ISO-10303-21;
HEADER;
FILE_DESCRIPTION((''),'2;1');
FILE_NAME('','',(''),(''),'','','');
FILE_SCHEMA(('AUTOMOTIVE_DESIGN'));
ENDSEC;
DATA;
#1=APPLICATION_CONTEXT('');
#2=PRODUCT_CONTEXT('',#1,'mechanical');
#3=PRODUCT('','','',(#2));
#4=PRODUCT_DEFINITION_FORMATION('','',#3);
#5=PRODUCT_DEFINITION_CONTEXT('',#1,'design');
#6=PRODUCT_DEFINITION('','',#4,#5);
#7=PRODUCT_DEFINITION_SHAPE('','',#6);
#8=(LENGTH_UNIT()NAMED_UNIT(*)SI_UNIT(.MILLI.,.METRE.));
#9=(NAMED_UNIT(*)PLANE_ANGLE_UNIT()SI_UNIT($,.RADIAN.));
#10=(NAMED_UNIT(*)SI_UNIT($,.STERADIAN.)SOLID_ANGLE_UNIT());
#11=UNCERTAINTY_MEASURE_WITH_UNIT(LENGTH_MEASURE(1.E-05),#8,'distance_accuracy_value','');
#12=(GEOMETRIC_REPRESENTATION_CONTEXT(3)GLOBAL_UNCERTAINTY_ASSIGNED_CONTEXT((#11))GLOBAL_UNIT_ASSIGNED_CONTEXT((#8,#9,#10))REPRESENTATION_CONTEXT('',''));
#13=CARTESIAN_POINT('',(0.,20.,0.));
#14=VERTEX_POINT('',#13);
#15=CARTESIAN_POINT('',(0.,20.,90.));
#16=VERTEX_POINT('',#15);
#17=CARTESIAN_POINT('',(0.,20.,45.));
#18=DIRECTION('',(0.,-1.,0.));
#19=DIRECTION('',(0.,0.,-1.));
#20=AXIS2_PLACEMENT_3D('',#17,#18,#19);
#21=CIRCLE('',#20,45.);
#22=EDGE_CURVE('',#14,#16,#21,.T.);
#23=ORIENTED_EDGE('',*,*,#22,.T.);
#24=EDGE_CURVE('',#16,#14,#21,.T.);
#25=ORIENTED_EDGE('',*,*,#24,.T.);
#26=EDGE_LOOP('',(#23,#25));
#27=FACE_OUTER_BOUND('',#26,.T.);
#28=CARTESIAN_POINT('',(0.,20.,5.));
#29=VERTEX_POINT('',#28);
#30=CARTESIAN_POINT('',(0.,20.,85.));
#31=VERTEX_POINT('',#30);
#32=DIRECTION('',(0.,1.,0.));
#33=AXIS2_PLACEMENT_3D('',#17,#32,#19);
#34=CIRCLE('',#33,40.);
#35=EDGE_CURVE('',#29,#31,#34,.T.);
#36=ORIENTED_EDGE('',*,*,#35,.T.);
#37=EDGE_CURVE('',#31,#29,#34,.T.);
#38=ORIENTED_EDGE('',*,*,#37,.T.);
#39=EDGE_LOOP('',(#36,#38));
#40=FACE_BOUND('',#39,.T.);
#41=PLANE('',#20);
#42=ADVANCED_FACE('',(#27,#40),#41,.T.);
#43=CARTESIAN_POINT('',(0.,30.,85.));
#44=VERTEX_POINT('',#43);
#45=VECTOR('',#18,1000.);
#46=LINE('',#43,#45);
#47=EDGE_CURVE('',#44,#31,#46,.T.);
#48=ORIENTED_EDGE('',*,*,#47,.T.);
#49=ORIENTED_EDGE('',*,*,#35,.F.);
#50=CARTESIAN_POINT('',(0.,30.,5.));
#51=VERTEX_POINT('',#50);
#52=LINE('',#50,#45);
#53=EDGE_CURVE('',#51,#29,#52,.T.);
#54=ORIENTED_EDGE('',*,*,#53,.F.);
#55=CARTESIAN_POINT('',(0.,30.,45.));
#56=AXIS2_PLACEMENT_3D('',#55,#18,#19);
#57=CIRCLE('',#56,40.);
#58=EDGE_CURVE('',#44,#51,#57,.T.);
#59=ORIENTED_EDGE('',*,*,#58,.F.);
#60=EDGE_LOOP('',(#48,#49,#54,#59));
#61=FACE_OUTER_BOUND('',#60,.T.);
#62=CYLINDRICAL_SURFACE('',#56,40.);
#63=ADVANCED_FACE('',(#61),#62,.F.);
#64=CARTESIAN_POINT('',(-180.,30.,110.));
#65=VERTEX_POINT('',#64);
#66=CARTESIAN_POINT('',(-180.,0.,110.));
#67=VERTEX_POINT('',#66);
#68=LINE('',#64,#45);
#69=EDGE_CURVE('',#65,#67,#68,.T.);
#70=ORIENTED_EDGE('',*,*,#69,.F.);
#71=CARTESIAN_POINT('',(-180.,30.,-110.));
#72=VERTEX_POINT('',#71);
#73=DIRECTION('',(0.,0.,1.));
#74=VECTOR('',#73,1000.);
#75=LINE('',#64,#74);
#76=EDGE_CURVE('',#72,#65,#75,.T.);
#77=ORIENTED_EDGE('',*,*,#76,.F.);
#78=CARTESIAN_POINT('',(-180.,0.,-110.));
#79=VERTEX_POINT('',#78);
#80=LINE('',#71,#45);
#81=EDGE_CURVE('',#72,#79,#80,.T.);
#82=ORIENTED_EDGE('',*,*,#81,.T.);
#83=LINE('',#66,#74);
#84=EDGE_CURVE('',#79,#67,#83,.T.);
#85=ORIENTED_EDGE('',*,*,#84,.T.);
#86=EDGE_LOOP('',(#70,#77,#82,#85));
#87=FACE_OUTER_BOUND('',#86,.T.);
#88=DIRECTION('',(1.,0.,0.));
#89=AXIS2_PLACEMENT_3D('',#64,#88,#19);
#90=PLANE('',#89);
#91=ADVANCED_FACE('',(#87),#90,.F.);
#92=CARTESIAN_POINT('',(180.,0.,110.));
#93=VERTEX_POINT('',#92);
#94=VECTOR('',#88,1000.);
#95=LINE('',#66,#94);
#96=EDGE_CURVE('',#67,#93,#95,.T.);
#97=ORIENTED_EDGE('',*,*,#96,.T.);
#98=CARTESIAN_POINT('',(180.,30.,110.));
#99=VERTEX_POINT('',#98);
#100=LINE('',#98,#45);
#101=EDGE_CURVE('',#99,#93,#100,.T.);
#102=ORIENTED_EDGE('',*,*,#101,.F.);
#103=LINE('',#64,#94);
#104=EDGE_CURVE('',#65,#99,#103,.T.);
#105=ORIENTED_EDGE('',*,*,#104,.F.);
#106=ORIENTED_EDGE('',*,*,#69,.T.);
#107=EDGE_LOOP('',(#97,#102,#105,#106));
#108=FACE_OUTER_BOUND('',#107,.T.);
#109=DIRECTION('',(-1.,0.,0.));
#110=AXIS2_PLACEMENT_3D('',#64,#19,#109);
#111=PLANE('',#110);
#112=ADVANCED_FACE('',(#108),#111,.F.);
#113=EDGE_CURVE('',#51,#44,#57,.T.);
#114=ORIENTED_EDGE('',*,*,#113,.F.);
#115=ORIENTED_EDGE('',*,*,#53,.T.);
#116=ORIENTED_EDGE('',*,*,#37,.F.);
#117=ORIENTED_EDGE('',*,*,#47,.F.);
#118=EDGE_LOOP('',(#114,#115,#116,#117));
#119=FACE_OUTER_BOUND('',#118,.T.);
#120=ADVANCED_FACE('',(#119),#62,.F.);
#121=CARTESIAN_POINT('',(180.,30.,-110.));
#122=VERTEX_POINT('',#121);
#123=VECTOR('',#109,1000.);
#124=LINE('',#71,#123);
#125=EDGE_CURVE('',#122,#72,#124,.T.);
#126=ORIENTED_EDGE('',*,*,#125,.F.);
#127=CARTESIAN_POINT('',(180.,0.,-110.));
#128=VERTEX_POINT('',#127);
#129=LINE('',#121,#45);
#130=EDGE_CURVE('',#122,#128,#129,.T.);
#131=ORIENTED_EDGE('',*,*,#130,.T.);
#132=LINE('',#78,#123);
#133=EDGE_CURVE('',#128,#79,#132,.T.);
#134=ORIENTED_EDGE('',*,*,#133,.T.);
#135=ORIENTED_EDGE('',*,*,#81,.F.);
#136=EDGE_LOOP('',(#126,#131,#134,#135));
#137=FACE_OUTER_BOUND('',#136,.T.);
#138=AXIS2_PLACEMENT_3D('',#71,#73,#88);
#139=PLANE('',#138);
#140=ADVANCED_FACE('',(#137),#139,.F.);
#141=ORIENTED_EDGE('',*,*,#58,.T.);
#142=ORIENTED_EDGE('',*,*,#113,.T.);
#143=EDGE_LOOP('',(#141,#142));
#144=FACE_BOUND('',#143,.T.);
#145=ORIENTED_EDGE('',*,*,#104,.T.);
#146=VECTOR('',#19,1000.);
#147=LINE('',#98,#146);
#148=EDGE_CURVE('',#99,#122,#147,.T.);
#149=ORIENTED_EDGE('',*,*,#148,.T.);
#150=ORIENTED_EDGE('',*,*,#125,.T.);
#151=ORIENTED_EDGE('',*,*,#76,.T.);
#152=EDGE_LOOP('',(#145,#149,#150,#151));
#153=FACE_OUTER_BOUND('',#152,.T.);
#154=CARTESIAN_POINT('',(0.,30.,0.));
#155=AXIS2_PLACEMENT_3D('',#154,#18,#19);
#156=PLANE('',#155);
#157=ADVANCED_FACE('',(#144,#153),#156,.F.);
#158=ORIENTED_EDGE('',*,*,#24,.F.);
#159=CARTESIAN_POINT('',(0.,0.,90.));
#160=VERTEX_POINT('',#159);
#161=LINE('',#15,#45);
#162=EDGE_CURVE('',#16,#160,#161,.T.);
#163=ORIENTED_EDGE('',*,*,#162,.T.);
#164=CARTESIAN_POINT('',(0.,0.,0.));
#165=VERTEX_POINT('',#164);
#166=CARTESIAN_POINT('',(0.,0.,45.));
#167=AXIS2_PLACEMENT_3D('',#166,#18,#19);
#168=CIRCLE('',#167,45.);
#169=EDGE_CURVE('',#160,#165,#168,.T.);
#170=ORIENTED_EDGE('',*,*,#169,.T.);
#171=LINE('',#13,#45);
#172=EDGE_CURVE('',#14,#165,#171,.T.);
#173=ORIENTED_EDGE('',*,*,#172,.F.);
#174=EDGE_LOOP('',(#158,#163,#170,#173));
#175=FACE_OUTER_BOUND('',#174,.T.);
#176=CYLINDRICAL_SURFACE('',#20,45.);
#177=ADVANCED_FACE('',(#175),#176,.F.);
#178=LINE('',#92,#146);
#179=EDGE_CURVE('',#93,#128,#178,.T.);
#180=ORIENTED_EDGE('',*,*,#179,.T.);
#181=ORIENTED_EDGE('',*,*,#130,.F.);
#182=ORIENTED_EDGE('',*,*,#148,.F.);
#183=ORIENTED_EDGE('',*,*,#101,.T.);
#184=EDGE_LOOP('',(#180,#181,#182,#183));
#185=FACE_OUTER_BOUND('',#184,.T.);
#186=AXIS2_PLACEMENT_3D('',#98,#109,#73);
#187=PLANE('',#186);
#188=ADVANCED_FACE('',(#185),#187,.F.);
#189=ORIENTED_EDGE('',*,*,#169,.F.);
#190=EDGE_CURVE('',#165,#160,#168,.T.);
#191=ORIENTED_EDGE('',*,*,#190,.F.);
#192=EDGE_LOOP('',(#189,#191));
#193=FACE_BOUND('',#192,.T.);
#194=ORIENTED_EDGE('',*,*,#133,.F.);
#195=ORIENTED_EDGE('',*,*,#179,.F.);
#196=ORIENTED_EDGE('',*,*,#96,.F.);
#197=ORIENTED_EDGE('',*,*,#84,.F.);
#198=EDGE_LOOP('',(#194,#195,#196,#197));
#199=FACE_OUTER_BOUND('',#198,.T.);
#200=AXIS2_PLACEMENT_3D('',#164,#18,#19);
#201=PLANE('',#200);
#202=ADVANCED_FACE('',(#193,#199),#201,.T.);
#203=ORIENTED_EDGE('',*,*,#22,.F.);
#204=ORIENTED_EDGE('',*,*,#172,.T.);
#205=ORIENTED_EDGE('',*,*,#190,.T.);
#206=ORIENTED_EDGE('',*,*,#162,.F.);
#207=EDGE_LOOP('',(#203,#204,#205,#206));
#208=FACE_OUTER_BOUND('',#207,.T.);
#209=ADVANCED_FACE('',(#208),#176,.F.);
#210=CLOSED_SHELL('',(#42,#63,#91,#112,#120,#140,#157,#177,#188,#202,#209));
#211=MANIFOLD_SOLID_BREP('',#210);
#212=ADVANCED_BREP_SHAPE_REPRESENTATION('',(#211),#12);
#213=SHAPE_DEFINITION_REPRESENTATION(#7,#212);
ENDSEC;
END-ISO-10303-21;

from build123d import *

# Parameters (mm, degrees)
SKETCH_1_W          = 360
SKETCH_1_H          = 220
EXTRUDE_1_DEPTH     = 30
SKETCH_2_R          = 40
CUT_EXTRUDE_1_DEPTH = 214.072757527
SKETCH_4_R          = 45
CUT_EXTRUDE_3_DEPTH = 20


with BuildPart() as part:
    # 草图1 → 凸台-拉伸1 (new body)
    with BuildSketch(Plane(origin=(0, 0, 0), x_dir=(1, 0, 0), z_dir=(0, 1, 0))):
        Rectangle(SKETCH_1_W, SKETCH_1_H)
    extrude(amount=EXTRUDE_1_DEPTH)

    # 草图2 → 切除-拉伸1 (cut, through all)
    with BuildSketch(Plane.XZ):
        with Locations(Location((0, 45, 0), (0, 0, 270))):
            Circle(SKETCH_2_R)
    extrude(amount=-CUT_EXTRUDE_1_DEPTH, mode=Mode.SUBTRACT)

    # 草图4 → 切除-拉伸3 (cut)
    with BuildSketch(Plane.XZ):
        with Locations(Location((0, 45, 0), (0, 0, 270))):
            Circle(SKETCH_4_R)
    extrude(amount=-CUT_EXTRUDE_3_DEPTH, mode=Mode.SUBTRACT)


solid = part.part
